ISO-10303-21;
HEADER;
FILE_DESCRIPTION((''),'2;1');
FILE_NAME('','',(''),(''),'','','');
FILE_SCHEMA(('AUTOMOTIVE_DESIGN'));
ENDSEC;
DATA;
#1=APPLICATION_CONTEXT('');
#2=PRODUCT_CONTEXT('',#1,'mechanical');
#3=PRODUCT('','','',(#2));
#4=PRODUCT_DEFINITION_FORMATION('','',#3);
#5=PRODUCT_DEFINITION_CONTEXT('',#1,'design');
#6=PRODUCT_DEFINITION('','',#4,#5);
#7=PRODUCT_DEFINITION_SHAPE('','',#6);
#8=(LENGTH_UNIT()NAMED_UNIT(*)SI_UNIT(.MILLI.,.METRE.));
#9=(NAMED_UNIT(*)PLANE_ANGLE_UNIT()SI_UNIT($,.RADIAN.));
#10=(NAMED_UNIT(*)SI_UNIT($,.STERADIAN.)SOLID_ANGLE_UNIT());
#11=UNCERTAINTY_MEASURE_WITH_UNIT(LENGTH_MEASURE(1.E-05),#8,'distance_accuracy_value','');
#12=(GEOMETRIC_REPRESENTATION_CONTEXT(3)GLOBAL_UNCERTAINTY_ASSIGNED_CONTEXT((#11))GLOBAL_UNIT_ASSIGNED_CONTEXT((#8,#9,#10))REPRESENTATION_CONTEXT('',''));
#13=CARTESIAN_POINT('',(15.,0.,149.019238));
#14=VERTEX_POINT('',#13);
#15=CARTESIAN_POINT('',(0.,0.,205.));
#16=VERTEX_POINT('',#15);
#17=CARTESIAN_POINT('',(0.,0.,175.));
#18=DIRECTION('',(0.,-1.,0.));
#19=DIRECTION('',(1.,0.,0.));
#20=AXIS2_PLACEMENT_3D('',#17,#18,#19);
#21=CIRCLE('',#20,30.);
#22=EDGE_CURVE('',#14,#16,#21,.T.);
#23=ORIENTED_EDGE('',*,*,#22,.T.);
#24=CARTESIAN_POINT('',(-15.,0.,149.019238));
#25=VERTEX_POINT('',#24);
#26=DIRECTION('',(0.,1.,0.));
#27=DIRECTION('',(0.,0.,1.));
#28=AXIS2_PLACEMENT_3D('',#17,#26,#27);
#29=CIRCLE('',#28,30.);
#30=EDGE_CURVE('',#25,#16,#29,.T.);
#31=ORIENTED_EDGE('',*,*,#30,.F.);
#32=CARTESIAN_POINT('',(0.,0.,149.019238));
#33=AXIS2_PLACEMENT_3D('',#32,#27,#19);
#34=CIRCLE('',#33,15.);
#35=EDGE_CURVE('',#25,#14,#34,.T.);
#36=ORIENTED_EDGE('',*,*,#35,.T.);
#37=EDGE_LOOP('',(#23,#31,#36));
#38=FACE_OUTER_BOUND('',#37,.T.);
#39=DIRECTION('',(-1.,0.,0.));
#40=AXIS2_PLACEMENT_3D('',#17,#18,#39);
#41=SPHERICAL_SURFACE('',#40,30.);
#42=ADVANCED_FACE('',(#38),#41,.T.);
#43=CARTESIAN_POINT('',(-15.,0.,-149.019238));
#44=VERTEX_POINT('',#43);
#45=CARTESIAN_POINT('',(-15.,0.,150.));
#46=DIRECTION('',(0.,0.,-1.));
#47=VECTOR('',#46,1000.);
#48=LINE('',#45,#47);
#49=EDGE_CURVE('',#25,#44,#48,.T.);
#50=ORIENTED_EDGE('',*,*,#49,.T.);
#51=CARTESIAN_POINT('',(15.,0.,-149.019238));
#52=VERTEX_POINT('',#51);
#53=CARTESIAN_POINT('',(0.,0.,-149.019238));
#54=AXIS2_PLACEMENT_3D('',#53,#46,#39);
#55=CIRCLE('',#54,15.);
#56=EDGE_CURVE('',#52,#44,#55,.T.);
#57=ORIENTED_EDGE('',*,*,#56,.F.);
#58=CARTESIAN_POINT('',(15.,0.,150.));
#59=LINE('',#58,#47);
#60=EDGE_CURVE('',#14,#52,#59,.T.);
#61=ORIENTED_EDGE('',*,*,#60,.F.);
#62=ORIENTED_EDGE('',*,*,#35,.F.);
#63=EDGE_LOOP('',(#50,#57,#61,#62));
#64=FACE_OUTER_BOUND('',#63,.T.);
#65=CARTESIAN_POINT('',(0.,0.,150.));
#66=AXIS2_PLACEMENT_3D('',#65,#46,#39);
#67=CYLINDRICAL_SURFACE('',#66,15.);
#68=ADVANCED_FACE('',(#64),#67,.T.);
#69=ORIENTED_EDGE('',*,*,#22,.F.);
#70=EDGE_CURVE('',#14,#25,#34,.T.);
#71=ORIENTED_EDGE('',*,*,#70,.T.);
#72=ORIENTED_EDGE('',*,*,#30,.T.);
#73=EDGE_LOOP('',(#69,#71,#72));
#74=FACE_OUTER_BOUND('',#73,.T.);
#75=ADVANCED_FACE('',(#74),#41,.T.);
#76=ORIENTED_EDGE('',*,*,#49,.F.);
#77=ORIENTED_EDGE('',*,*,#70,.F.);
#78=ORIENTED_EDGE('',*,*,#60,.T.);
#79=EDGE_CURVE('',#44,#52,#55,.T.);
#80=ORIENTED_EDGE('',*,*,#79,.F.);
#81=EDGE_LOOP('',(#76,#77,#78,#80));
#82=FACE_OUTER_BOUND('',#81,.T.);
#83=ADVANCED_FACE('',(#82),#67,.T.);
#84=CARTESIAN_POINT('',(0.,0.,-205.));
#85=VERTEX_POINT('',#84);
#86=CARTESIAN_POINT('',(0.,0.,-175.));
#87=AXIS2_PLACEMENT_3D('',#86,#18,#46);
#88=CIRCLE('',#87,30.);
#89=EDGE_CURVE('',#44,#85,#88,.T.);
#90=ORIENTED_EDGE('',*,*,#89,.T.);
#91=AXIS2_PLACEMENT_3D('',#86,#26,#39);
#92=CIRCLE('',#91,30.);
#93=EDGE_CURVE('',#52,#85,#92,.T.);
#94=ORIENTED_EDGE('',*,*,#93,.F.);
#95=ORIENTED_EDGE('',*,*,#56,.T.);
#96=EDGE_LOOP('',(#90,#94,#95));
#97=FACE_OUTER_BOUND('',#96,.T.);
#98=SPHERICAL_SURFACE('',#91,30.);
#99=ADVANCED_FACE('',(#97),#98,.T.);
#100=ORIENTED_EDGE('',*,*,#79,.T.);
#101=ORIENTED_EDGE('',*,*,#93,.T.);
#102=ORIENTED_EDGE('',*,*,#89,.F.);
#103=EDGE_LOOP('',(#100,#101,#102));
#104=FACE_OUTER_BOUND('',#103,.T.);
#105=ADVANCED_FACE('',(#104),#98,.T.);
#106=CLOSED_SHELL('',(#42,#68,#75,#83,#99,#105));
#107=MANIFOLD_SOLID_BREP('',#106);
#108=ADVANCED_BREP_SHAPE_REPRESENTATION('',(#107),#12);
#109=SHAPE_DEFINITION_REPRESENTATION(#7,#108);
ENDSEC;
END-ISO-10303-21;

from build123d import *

# Parameters (mm, degrees)
SKETCH1_R           = 15
BOSS_EXTRUDE1_DEPTH = 150


with BuildPart() as part:
    # Sketch1 → Boss-Extrude1 (new, symmetric)
    with BuildSketch(Plane.XY):
        Circle(SKETCH1_R)
    extrude(amount=BOSS_EXTRUDE1_DEPTH, both=True)

    # Sketch2 → Revolve1 (revolve)
    with BuildSketch(Plane(origin=(0, 0, 0), x_dir=(1, 0, 0), z_dir=(0, 1, 0))):
        with BuildLine():
            Line((0, 205), (0, 145))
            ThreePointArc((0, 145), (30, 175), (0, 205))
        make_face()
    revolve1 = revolve(axis=Axis((0, 0, -205), (0, 0, 1)))

    # Mirror1: Revolve1 across plane
    add(revolve1.mirror(Plane.XY))


solid = part.part
